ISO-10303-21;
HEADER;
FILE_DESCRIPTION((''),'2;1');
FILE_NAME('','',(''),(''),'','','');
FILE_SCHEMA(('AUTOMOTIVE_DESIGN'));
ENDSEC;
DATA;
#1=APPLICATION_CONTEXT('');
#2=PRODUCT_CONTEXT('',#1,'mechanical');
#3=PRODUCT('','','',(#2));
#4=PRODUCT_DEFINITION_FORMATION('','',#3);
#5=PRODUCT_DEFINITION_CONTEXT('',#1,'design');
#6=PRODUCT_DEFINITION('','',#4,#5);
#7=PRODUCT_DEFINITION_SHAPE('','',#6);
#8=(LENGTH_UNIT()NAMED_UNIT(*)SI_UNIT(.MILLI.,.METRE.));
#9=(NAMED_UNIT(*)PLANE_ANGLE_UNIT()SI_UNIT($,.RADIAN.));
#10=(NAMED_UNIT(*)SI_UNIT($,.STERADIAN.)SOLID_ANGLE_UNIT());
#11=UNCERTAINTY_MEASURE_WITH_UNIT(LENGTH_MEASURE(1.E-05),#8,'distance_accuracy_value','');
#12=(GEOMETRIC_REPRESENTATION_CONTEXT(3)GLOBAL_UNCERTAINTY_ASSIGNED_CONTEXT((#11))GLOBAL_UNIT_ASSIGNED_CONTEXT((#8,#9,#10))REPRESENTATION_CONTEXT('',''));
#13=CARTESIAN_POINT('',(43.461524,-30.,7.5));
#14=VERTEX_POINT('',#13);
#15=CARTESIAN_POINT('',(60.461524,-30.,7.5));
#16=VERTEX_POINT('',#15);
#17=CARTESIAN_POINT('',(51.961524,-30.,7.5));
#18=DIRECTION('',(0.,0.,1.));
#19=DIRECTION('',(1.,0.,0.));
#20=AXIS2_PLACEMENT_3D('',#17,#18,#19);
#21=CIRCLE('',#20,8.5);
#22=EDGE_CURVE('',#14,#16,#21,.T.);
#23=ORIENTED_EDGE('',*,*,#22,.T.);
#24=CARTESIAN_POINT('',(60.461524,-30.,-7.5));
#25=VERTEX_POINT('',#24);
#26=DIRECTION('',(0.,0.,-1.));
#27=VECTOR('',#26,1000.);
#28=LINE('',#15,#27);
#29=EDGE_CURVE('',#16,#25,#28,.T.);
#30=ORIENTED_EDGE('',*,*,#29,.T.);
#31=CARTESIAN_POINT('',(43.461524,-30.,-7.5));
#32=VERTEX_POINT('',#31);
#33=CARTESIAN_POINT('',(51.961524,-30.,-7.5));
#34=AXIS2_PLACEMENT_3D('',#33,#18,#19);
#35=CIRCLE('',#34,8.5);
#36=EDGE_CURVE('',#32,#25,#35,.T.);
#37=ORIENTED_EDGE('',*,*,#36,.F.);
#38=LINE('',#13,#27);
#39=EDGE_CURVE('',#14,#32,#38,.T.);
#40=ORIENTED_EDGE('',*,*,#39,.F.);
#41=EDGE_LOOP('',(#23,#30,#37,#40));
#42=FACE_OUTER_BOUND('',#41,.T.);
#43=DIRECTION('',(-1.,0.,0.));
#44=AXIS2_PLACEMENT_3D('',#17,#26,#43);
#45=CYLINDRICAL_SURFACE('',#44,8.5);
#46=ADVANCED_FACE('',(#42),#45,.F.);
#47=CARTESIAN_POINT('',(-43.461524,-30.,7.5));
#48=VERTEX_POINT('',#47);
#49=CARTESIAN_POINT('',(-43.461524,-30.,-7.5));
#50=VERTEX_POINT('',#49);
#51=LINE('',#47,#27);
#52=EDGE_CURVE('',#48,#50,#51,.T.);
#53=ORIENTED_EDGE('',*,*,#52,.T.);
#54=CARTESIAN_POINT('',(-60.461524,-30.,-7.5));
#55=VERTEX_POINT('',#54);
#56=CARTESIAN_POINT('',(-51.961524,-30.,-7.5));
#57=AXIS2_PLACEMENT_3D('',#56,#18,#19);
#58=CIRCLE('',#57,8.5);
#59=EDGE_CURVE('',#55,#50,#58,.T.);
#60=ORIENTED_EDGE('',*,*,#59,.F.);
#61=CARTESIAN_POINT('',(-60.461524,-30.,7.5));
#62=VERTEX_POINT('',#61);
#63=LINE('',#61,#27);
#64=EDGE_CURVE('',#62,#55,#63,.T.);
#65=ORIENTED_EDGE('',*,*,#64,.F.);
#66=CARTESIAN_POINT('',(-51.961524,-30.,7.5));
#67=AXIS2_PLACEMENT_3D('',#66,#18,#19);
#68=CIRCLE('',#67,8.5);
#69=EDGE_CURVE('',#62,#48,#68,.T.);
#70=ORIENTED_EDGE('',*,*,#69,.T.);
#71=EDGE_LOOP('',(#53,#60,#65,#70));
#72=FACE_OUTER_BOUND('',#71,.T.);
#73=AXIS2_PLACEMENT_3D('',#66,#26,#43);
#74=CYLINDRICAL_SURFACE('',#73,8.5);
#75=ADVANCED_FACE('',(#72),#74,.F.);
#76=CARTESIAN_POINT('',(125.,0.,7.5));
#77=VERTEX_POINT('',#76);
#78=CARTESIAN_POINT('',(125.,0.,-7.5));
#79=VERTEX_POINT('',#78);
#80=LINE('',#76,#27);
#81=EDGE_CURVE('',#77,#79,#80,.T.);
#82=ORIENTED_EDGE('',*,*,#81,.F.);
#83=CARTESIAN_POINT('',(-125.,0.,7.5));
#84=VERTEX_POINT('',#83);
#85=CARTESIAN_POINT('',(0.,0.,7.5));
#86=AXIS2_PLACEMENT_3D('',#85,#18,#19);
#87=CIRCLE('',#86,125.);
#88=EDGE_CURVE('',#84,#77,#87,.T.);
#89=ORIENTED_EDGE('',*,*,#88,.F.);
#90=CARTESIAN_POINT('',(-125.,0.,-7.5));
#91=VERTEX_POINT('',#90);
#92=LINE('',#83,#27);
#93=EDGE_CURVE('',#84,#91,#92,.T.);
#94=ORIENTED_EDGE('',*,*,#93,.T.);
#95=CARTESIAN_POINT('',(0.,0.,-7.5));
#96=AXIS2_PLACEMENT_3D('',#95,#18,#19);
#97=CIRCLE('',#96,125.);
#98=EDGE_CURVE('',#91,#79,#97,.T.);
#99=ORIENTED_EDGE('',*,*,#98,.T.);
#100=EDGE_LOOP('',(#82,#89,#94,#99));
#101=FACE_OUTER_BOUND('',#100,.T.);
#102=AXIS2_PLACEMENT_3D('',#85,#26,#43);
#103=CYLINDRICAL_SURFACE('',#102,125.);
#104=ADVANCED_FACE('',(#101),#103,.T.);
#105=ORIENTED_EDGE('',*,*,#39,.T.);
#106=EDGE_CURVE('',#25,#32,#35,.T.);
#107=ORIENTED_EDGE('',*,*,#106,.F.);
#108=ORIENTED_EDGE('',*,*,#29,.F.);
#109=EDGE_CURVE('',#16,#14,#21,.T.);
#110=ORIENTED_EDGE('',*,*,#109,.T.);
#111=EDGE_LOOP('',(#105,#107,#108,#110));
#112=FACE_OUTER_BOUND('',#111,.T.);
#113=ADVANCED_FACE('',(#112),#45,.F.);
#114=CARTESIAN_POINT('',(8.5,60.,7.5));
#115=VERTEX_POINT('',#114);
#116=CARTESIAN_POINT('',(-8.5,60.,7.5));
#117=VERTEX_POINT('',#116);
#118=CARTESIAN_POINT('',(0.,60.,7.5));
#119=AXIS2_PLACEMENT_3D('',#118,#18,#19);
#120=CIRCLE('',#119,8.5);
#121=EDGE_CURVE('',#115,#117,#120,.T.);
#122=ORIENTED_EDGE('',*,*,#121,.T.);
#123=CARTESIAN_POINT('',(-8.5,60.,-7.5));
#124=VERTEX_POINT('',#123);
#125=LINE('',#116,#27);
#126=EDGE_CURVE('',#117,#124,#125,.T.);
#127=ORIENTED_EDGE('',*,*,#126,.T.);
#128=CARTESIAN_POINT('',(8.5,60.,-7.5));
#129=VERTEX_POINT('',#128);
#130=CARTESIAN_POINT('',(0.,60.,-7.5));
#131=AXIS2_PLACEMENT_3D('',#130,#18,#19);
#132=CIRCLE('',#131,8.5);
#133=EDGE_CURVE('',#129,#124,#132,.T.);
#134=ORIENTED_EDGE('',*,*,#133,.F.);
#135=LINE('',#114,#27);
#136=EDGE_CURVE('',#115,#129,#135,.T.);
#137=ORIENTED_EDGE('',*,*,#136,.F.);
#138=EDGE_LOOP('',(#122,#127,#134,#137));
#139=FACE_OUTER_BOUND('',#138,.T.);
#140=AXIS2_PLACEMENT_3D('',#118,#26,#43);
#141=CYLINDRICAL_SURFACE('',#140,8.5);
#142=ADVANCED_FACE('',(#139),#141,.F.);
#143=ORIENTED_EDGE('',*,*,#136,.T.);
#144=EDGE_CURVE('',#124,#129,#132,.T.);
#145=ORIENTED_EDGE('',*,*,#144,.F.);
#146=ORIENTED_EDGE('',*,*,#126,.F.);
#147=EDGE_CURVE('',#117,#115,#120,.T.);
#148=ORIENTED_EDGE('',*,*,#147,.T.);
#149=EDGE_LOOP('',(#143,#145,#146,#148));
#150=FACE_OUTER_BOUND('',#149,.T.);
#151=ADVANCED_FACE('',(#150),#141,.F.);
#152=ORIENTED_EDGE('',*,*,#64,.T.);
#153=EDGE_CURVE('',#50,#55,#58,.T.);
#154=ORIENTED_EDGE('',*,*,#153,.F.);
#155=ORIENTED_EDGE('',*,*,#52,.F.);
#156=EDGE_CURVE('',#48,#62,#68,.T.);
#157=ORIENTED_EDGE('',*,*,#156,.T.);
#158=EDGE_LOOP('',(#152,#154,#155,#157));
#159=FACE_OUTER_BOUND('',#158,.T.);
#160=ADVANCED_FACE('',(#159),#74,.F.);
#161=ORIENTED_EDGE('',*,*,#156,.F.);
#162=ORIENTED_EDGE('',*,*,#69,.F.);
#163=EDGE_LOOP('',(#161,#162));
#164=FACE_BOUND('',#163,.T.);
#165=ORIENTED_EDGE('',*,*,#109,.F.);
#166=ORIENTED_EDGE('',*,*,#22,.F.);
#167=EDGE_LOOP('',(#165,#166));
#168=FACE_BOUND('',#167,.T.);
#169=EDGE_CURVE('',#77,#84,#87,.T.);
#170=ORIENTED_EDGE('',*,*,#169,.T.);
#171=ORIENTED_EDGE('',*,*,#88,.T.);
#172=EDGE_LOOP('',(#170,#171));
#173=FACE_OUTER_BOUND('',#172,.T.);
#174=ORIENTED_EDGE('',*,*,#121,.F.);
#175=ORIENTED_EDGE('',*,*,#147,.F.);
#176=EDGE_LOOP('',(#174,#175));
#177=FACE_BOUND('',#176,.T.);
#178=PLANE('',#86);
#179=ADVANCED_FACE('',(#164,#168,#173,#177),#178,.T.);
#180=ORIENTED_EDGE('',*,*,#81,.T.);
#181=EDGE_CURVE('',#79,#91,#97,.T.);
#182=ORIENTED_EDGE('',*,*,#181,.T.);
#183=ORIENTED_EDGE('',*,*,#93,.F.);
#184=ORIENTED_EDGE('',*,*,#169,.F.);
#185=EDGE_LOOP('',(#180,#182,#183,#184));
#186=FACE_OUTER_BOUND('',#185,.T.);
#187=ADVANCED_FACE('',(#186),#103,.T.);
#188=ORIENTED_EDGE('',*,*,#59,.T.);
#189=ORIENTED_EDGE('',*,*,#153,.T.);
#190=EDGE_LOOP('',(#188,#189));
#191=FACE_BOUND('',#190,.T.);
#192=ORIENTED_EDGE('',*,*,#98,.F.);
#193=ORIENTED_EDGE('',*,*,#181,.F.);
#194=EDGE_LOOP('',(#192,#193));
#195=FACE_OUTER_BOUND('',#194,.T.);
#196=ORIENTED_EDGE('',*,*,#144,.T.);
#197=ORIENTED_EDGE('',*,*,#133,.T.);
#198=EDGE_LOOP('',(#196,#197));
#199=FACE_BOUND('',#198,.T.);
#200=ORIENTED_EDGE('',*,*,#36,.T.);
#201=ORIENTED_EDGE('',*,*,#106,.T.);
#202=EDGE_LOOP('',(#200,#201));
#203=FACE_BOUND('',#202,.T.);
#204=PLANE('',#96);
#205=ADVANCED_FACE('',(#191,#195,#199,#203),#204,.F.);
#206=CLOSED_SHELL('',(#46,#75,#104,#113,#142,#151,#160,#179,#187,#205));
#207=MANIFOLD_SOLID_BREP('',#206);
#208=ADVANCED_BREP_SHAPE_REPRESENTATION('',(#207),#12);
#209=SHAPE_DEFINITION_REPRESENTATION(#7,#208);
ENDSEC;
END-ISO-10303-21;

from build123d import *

# Parameters (mm, degrees)
SKETCH1_R           = 125
SKETCH1_R_2         = 8.5
BOSS_EXTRUDE1_DEPTH = 7.5


with BuildPart() as part:
    # Sketch1 → Boss-Extrude1 (new, symmetric)
    with BuildSketch(Plane.XY):
        Circle(SKETCH1_R)
        with Locations((0, 60)):
            Circle(SKETCH1_R_2, mode=Mode.SUBTRACT)
        with Locations((51.961524227, -30)):
            Circle(SKETCH1_R_2, mode=Mode.SUBTRACT)
        with Locations((-51.961524227, -30)):
            Circle(SKETCH1_R_2, mode=Mode.SUBTRACT)
    extrude(amount=BOSS_EXTRUDE1_DEPTH, both=True)


solid = part.part
